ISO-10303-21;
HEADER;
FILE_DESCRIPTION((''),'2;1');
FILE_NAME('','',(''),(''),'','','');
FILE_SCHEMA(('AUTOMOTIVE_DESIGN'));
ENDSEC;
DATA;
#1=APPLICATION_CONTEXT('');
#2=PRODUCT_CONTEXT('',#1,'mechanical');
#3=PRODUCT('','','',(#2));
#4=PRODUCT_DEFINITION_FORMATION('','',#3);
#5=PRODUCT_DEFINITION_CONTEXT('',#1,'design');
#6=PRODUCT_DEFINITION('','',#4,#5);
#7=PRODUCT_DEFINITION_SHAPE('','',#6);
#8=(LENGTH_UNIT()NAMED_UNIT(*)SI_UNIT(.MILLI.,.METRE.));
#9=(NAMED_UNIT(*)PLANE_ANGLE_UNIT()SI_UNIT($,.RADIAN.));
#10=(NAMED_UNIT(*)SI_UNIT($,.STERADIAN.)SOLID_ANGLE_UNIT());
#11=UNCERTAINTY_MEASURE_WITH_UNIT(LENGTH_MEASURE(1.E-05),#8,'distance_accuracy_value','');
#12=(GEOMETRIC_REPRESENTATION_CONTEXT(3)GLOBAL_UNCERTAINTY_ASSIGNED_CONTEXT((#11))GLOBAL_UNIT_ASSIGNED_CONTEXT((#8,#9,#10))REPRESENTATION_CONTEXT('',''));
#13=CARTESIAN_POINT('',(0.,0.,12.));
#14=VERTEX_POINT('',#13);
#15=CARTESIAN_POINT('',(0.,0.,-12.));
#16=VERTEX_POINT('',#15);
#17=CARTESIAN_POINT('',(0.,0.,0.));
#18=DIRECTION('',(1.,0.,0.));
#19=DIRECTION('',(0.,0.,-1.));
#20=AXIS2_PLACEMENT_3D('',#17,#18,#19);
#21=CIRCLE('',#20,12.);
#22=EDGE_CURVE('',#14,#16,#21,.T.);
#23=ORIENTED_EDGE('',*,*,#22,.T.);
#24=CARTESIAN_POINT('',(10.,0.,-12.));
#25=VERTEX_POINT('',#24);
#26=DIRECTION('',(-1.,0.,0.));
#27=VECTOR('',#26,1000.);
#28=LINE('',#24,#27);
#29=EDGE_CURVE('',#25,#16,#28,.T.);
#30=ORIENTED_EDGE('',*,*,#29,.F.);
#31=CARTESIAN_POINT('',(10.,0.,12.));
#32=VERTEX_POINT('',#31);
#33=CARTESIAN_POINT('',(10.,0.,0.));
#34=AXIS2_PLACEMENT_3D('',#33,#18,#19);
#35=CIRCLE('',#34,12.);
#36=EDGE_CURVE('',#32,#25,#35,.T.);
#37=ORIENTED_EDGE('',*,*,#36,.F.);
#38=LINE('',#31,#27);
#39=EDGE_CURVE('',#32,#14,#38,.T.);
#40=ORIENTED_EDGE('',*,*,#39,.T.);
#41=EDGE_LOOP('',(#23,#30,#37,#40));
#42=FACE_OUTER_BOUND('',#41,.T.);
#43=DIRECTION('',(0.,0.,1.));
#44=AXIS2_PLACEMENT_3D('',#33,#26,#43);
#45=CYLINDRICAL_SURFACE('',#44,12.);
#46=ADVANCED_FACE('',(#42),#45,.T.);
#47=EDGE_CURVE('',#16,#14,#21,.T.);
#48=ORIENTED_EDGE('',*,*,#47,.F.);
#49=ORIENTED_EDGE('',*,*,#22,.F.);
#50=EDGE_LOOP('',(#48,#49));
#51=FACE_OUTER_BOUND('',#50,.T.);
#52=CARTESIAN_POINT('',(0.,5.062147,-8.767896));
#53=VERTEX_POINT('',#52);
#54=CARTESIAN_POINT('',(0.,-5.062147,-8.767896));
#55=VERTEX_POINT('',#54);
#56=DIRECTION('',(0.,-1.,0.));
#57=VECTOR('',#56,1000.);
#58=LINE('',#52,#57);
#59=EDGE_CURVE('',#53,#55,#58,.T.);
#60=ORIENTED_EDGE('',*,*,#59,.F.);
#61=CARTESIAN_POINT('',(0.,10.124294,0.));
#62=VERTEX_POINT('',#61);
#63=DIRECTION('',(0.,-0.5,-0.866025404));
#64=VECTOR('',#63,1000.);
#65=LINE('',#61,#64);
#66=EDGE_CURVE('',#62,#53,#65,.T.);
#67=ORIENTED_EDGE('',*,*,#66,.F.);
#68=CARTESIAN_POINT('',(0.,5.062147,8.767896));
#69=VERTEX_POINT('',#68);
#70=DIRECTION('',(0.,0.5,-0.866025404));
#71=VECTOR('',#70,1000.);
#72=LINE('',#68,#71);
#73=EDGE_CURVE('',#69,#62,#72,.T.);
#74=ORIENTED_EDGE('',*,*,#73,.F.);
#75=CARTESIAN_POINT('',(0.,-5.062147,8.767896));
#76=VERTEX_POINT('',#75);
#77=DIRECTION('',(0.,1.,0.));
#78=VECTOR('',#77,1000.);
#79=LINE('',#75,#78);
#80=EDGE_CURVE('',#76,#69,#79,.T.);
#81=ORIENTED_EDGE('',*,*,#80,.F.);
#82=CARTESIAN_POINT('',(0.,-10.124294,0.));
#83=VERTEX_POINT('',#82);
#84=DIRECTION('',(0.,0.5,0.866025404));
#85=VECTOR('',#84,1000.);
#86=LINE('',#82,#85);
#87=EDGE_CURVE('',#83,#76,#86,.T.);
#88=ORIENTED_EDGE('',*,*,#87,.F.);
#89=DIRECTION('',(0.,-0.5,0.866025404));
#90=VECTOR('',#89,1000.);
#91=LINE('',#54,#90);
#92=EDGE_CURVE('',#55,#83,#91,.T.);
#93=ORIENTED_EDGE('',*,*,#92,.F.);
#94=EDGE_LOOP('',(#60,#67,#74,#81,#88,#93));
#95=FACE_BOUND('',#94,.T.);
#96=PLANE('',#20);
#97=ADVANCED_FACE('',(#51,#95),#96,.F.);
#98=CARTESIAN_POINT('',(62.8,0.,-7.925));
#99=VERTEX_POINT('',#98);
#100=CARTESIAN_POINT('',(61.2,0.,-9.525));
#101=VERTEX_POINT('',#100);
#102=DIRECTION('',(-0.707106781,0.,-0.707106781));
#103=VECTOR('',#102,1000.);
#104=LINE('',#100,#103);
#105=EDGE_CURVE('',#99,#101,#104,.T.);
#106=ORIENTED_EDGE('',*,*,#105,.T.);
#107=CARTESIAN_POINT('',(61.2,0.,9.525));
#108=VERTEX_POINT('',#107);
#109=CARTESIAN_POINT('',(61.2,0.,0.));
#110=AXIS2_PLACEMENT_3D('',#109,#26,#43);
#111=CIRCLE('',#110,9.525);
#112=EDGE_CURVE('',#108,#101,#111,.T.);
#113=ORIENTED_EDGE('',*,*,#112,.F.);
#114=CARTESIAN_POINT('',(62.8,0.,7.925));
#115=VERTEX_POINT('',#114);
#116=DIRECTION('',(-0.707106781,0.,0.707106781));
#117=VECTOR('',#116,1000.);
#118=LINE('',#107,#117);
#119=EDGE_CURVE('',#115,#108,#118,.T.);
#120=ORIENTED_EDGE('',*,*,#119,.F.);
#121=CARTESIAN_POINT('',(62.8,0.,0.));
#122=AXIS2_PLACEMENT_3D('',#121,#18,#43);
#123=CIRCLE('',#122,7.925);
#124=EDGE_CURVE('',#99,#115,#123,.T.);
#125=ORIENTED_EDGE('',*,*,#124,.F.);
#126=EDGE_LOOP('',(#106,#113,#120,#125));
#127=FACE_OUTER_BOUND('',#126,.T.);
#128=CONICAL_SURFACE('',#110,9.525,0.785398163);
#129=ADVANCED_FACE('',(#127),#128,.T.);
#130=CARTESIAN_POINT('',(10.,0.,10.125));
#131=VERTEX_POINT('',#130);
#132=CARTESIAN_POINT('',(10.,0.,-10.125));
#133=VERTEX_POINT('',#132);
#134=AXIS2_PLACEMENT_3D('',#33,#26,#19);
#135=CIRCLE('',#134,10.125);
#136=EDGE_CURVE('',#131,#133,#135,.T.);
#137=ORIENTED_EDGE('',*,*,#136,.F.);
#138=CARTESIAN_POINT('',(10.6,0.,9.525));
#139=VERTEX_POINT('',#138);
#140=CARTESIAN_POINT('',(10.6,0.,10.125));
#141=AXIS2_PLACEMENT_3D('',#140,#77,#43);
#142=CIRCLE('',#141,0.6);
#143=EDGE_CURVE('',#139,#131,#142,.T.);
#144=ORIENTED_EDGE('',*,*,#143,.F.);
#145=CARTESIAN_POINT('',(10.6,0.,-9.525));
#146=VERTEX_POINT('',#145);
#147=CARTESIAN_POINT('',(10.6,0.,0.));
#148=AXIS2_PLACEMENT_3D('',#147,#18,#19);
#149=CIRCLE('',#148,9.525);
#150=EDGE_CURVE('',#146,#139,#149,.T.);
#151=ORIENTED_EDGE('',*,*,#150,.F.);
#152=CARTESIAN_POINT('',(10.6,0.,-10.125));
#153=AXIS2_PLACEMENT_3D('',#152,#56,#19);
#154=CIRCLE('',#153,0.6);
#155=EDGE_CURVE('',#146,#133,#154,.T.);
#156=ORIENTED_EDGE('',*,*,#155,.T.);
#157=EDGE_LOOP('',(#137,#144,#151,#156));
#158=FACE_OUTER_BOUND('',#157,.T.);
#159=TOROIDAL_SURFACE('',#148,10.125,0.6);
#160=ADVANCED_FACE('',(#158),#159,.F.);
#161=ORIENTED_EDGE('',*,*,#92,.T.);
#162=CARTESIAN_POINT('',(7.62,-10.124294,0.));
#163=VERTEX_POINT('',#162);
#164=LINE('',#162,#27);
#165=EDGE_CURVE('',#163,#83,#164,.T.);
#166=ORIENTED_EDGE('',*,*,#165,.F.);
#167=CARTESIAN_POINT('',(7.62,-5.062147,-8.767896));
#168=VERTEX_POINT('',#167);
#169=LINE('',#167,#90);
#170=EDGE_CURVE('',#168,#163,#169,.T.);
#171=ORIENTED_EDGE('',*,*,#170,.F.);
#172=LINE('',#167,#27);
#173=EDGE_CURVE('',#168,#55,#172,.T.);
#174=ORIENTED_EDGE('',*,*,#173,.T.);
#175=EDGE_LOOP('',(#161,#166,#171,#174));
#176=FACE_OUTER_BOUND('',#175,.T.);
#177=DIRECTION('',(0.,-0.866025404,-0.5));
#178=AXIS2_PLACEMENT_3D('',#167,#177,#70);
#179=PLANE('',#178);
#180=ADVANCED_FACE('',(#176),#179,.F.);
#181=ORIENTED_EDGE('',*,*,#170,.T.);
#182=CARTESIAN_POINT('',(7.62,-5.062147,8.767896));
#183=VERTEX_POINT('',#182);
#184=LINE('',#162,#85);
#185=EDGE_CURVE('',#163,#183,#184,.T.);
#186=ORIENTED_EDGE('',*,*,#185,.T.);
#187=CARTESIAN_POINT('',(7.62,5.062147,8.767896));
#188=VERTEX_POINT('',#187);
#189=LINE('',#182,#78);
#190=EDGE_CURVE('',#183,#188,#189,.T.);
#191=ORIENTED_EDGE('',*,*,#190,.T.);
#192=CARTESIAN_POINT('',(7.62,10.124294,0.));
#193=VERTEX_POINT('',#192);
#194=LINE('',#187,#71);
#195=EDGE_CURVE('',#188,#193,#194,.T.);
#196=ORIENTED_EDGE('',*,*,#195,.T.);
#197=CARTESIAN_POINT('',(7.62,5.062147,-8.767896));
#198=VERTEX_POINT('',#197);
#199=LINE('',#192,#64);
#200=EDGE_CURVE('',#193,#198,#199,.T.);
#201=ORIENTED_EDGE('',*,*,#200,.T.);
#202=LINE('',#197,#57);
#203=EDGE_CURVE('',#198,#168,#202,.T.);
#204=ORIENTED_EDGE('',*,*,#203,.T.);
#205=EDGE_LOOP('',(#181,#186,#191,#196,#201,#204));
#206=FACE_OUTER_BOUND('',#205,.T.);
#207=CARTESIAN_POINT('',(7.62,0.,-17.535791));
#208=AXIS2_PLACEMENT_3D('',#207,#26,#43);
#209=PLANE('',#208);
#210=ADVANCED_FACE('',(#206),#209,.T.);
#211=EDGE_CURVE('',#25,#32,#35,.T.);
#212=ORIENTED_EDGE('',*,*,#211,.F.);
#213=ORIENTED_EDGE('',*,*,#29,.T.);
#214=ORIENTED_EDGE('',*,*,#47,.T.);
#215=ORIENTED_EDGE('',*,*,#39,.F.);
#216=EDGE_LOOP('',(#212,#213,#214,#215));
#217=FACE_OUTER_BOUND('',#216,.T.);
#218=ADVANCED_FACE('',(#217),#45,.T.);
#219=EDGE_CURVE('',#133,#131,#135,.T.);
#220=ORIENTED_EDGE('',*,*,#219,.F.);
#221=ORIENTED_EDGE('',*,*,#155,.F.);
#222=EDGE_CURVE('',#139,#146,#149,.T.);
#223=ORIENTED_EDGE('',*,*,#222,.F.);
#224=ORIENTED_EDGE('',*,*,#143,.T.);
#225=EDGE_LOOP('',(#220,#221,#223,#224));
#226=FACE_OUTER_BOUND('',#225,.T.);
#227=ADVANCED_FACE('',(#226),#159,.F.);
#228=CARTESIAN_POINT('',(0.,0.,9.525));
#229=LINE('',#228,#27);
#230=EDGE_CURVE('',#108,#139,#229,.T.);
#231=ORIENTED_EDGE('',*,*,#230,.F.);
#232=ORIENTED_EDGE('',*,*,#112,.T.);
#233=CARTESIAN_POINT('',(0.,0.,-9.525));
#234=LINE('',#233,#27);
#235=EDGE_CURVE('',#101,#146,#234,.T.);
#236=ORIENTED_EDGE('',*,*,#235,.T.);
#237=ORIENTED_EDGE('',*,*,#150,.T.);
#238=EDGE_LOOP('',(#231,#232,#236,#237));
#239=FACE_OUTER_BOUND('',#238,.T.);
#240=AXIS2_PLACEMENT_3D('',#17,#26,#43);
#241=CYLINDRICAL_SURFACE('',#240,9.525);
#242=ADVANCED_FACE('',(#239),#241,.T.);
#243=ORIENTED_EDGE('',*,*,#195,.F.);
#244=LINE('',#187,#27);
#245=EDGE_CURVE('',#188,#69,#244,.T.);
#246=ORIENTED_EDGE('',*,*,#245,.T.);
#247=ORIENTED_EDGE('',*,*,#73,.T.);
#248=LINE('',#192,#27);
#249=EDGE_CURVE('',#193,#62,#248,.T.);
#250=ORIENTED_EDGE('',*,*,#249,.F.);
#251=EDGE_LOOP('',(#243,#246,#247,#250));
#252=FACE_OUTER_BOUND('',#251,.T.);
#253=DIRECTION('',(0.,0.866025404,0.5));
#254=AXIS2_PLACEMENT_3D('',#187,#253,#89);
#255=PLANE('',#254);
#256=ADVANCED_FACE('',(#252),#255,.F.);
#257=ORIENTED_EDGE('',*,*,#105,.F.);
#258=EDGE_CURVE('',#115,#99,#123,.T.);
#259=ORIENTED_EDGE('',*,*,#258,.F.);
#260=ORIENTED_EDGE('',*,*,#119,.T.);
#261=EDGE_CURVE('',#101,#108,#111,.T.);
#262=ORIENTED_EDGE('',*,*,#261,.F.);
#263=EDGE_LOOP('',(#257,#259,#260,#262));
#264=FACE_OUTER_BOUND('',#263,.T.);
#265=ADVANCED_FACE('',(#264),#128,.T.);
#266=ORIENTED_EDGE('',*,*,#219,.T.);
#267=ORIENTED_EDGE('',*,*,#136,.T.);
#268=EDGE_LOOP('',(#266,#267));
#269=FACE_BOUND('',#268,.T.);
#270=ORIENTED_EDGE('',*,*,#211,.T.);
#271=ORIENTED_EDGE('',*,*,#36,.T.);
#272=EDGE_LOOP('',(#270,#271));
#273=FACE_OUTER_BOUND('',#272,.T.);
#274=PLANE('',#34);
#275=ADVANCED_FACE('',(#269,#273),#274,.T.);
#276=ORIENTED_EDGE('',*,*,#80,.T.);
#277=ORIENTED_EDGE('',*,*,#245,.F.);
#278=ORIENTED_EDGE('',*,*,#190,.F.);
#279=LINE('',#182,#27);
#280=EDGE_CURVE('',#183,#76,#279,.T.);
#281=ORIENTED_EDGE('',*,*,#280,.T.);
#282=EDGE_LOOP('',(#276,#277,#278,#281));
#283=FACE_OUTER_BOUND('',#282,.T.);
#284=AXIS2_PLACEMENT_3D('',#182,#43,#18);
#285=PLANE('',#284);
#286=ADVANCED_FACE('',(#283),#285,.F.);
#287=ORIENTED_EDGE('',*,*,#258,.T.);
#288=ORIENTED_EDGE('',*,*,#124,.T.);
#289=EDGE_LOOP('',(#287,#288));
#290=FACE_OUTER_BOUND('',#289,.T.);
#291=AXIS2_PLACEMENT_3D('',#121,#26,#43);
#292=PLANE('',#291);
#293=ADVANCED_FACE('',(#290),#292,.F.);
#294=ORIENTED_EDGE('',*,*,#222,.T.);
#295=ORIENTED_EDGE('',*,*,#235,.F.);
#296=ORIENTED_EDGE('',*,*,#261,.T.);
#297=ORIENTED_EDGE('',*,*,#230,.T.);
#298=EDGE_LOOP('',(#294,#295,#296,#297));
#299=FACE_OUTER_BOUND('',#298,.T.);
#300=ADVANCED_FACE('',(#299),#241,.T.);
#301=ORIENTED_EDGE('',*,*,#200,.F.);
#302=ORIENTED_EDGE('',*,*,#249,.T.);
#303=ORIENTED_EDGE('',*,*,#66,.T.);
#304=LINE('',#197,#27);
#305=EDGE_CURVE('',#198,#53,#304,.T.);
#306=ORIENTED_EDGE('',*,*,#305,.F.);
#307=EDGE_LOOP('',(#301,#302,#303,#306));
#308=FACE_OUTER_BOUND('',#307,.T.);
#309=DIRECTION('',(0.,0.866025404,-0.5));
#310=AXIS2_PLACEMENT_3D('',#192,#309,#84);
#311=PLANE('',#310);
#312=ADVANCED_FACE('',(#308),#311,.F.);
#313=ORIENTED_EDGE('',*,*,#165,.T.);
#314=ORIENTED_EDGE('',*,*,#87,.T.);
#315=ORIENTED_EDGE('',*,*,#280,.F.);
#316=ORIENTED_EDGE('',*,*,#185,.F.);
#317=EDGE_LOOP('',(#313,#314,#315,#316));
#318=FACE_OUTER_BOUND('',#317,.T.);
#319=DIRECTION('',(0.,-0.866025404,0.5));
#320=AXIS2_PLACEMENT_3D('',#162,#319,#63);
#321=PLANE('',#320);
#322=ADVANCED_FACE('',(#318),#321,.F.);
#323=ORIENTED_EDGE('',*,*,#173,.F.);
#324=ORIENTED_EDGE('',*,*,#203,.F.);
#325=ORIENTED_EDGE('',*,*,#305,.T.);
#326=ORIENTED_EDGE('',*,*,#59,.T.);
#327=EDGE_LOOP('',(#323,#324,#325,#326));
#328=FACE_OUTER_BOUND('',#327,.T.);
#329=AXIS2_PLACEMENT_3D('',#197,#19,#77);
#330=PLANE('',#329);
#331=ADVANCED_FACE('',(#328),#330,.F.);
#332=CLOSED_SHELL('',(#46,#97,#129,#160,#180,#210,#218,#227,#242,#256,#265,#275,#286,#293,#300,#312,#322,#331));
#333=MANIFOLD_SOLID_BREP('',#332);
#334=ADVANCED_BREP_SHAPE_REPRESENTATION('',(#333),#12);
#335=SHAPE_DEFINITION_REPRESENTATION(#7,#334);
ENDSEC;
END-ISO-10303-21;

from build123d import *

# Parameters (mm, degrees)
SKETCH1_R          = 12
BASE_EXTRUDE_DEPTH = 10
CHAMFER_2_SIZE     = 1.6
FILLET_2_R         = 0.6
CUT_EXTRUDE1_DEPTH = 7.62


with BuildPart() as part:
    # Sketch1 → Base-Extrude (new body)
    with BuildSketch(Plane(origin=(0, 0, 0), x_dir=(0, 0, -1), z_dir=(1, 0, 0))):
        Circle(SKETCH1_R)
    extrude(amount=BASE_EXTRUDE_DEPTH)

    # Sketch2 → Boss-Revolve1 (revolve)
    with BuildSketch(Plane.XY, mode=Mode.PRIVATE) as boss_revolve1_sk:
        Polygon((0, 0), (62.8, 0), (62.8, 6.268), (62.8, 9.525), (27.8072, 9.525), (0, 9.525), align=None)
    revolve(boss_revolve1_sk.sketch.rotate(Axis((0, 0, 0), (1, 0, 0)), 90), axis=Axis((0, 0, 0), (1, 0, 0)))

    # Chamfer 2
    chamfer_2_edges = [part.edges().sort_by_distance(p)[0] for p in [
        (62.8, 0, -9.525),
    ]]
    chamfer(chamfer_2_edges, length=CHAMFER_2_SIZE)

    # Fillet 2
    fillet_2_edges = [part.edges().sort_by_distance(p)[0] for p in [
        (10, 0, -9.525),
    ]]
    fillet(fillet_2_edges, radius=FILLET_2_R)

    # Sketch7 → Cut-Extrude1 (cut)
    with BuildSketch(Plane.ZY):
        Polygon((-8.76789552, 5.062146839), (-8.76789552, -5.062146839), (0, -10.124293677), (8.76789552, -5.062146839), (8.76789552, 5.062146839), (0, 10.124293677), align=None)
    extrude(amount=-CUT_EXTRUDE1_DEPTH, mode=Mode.SUBTRACT)


solid = part.part
